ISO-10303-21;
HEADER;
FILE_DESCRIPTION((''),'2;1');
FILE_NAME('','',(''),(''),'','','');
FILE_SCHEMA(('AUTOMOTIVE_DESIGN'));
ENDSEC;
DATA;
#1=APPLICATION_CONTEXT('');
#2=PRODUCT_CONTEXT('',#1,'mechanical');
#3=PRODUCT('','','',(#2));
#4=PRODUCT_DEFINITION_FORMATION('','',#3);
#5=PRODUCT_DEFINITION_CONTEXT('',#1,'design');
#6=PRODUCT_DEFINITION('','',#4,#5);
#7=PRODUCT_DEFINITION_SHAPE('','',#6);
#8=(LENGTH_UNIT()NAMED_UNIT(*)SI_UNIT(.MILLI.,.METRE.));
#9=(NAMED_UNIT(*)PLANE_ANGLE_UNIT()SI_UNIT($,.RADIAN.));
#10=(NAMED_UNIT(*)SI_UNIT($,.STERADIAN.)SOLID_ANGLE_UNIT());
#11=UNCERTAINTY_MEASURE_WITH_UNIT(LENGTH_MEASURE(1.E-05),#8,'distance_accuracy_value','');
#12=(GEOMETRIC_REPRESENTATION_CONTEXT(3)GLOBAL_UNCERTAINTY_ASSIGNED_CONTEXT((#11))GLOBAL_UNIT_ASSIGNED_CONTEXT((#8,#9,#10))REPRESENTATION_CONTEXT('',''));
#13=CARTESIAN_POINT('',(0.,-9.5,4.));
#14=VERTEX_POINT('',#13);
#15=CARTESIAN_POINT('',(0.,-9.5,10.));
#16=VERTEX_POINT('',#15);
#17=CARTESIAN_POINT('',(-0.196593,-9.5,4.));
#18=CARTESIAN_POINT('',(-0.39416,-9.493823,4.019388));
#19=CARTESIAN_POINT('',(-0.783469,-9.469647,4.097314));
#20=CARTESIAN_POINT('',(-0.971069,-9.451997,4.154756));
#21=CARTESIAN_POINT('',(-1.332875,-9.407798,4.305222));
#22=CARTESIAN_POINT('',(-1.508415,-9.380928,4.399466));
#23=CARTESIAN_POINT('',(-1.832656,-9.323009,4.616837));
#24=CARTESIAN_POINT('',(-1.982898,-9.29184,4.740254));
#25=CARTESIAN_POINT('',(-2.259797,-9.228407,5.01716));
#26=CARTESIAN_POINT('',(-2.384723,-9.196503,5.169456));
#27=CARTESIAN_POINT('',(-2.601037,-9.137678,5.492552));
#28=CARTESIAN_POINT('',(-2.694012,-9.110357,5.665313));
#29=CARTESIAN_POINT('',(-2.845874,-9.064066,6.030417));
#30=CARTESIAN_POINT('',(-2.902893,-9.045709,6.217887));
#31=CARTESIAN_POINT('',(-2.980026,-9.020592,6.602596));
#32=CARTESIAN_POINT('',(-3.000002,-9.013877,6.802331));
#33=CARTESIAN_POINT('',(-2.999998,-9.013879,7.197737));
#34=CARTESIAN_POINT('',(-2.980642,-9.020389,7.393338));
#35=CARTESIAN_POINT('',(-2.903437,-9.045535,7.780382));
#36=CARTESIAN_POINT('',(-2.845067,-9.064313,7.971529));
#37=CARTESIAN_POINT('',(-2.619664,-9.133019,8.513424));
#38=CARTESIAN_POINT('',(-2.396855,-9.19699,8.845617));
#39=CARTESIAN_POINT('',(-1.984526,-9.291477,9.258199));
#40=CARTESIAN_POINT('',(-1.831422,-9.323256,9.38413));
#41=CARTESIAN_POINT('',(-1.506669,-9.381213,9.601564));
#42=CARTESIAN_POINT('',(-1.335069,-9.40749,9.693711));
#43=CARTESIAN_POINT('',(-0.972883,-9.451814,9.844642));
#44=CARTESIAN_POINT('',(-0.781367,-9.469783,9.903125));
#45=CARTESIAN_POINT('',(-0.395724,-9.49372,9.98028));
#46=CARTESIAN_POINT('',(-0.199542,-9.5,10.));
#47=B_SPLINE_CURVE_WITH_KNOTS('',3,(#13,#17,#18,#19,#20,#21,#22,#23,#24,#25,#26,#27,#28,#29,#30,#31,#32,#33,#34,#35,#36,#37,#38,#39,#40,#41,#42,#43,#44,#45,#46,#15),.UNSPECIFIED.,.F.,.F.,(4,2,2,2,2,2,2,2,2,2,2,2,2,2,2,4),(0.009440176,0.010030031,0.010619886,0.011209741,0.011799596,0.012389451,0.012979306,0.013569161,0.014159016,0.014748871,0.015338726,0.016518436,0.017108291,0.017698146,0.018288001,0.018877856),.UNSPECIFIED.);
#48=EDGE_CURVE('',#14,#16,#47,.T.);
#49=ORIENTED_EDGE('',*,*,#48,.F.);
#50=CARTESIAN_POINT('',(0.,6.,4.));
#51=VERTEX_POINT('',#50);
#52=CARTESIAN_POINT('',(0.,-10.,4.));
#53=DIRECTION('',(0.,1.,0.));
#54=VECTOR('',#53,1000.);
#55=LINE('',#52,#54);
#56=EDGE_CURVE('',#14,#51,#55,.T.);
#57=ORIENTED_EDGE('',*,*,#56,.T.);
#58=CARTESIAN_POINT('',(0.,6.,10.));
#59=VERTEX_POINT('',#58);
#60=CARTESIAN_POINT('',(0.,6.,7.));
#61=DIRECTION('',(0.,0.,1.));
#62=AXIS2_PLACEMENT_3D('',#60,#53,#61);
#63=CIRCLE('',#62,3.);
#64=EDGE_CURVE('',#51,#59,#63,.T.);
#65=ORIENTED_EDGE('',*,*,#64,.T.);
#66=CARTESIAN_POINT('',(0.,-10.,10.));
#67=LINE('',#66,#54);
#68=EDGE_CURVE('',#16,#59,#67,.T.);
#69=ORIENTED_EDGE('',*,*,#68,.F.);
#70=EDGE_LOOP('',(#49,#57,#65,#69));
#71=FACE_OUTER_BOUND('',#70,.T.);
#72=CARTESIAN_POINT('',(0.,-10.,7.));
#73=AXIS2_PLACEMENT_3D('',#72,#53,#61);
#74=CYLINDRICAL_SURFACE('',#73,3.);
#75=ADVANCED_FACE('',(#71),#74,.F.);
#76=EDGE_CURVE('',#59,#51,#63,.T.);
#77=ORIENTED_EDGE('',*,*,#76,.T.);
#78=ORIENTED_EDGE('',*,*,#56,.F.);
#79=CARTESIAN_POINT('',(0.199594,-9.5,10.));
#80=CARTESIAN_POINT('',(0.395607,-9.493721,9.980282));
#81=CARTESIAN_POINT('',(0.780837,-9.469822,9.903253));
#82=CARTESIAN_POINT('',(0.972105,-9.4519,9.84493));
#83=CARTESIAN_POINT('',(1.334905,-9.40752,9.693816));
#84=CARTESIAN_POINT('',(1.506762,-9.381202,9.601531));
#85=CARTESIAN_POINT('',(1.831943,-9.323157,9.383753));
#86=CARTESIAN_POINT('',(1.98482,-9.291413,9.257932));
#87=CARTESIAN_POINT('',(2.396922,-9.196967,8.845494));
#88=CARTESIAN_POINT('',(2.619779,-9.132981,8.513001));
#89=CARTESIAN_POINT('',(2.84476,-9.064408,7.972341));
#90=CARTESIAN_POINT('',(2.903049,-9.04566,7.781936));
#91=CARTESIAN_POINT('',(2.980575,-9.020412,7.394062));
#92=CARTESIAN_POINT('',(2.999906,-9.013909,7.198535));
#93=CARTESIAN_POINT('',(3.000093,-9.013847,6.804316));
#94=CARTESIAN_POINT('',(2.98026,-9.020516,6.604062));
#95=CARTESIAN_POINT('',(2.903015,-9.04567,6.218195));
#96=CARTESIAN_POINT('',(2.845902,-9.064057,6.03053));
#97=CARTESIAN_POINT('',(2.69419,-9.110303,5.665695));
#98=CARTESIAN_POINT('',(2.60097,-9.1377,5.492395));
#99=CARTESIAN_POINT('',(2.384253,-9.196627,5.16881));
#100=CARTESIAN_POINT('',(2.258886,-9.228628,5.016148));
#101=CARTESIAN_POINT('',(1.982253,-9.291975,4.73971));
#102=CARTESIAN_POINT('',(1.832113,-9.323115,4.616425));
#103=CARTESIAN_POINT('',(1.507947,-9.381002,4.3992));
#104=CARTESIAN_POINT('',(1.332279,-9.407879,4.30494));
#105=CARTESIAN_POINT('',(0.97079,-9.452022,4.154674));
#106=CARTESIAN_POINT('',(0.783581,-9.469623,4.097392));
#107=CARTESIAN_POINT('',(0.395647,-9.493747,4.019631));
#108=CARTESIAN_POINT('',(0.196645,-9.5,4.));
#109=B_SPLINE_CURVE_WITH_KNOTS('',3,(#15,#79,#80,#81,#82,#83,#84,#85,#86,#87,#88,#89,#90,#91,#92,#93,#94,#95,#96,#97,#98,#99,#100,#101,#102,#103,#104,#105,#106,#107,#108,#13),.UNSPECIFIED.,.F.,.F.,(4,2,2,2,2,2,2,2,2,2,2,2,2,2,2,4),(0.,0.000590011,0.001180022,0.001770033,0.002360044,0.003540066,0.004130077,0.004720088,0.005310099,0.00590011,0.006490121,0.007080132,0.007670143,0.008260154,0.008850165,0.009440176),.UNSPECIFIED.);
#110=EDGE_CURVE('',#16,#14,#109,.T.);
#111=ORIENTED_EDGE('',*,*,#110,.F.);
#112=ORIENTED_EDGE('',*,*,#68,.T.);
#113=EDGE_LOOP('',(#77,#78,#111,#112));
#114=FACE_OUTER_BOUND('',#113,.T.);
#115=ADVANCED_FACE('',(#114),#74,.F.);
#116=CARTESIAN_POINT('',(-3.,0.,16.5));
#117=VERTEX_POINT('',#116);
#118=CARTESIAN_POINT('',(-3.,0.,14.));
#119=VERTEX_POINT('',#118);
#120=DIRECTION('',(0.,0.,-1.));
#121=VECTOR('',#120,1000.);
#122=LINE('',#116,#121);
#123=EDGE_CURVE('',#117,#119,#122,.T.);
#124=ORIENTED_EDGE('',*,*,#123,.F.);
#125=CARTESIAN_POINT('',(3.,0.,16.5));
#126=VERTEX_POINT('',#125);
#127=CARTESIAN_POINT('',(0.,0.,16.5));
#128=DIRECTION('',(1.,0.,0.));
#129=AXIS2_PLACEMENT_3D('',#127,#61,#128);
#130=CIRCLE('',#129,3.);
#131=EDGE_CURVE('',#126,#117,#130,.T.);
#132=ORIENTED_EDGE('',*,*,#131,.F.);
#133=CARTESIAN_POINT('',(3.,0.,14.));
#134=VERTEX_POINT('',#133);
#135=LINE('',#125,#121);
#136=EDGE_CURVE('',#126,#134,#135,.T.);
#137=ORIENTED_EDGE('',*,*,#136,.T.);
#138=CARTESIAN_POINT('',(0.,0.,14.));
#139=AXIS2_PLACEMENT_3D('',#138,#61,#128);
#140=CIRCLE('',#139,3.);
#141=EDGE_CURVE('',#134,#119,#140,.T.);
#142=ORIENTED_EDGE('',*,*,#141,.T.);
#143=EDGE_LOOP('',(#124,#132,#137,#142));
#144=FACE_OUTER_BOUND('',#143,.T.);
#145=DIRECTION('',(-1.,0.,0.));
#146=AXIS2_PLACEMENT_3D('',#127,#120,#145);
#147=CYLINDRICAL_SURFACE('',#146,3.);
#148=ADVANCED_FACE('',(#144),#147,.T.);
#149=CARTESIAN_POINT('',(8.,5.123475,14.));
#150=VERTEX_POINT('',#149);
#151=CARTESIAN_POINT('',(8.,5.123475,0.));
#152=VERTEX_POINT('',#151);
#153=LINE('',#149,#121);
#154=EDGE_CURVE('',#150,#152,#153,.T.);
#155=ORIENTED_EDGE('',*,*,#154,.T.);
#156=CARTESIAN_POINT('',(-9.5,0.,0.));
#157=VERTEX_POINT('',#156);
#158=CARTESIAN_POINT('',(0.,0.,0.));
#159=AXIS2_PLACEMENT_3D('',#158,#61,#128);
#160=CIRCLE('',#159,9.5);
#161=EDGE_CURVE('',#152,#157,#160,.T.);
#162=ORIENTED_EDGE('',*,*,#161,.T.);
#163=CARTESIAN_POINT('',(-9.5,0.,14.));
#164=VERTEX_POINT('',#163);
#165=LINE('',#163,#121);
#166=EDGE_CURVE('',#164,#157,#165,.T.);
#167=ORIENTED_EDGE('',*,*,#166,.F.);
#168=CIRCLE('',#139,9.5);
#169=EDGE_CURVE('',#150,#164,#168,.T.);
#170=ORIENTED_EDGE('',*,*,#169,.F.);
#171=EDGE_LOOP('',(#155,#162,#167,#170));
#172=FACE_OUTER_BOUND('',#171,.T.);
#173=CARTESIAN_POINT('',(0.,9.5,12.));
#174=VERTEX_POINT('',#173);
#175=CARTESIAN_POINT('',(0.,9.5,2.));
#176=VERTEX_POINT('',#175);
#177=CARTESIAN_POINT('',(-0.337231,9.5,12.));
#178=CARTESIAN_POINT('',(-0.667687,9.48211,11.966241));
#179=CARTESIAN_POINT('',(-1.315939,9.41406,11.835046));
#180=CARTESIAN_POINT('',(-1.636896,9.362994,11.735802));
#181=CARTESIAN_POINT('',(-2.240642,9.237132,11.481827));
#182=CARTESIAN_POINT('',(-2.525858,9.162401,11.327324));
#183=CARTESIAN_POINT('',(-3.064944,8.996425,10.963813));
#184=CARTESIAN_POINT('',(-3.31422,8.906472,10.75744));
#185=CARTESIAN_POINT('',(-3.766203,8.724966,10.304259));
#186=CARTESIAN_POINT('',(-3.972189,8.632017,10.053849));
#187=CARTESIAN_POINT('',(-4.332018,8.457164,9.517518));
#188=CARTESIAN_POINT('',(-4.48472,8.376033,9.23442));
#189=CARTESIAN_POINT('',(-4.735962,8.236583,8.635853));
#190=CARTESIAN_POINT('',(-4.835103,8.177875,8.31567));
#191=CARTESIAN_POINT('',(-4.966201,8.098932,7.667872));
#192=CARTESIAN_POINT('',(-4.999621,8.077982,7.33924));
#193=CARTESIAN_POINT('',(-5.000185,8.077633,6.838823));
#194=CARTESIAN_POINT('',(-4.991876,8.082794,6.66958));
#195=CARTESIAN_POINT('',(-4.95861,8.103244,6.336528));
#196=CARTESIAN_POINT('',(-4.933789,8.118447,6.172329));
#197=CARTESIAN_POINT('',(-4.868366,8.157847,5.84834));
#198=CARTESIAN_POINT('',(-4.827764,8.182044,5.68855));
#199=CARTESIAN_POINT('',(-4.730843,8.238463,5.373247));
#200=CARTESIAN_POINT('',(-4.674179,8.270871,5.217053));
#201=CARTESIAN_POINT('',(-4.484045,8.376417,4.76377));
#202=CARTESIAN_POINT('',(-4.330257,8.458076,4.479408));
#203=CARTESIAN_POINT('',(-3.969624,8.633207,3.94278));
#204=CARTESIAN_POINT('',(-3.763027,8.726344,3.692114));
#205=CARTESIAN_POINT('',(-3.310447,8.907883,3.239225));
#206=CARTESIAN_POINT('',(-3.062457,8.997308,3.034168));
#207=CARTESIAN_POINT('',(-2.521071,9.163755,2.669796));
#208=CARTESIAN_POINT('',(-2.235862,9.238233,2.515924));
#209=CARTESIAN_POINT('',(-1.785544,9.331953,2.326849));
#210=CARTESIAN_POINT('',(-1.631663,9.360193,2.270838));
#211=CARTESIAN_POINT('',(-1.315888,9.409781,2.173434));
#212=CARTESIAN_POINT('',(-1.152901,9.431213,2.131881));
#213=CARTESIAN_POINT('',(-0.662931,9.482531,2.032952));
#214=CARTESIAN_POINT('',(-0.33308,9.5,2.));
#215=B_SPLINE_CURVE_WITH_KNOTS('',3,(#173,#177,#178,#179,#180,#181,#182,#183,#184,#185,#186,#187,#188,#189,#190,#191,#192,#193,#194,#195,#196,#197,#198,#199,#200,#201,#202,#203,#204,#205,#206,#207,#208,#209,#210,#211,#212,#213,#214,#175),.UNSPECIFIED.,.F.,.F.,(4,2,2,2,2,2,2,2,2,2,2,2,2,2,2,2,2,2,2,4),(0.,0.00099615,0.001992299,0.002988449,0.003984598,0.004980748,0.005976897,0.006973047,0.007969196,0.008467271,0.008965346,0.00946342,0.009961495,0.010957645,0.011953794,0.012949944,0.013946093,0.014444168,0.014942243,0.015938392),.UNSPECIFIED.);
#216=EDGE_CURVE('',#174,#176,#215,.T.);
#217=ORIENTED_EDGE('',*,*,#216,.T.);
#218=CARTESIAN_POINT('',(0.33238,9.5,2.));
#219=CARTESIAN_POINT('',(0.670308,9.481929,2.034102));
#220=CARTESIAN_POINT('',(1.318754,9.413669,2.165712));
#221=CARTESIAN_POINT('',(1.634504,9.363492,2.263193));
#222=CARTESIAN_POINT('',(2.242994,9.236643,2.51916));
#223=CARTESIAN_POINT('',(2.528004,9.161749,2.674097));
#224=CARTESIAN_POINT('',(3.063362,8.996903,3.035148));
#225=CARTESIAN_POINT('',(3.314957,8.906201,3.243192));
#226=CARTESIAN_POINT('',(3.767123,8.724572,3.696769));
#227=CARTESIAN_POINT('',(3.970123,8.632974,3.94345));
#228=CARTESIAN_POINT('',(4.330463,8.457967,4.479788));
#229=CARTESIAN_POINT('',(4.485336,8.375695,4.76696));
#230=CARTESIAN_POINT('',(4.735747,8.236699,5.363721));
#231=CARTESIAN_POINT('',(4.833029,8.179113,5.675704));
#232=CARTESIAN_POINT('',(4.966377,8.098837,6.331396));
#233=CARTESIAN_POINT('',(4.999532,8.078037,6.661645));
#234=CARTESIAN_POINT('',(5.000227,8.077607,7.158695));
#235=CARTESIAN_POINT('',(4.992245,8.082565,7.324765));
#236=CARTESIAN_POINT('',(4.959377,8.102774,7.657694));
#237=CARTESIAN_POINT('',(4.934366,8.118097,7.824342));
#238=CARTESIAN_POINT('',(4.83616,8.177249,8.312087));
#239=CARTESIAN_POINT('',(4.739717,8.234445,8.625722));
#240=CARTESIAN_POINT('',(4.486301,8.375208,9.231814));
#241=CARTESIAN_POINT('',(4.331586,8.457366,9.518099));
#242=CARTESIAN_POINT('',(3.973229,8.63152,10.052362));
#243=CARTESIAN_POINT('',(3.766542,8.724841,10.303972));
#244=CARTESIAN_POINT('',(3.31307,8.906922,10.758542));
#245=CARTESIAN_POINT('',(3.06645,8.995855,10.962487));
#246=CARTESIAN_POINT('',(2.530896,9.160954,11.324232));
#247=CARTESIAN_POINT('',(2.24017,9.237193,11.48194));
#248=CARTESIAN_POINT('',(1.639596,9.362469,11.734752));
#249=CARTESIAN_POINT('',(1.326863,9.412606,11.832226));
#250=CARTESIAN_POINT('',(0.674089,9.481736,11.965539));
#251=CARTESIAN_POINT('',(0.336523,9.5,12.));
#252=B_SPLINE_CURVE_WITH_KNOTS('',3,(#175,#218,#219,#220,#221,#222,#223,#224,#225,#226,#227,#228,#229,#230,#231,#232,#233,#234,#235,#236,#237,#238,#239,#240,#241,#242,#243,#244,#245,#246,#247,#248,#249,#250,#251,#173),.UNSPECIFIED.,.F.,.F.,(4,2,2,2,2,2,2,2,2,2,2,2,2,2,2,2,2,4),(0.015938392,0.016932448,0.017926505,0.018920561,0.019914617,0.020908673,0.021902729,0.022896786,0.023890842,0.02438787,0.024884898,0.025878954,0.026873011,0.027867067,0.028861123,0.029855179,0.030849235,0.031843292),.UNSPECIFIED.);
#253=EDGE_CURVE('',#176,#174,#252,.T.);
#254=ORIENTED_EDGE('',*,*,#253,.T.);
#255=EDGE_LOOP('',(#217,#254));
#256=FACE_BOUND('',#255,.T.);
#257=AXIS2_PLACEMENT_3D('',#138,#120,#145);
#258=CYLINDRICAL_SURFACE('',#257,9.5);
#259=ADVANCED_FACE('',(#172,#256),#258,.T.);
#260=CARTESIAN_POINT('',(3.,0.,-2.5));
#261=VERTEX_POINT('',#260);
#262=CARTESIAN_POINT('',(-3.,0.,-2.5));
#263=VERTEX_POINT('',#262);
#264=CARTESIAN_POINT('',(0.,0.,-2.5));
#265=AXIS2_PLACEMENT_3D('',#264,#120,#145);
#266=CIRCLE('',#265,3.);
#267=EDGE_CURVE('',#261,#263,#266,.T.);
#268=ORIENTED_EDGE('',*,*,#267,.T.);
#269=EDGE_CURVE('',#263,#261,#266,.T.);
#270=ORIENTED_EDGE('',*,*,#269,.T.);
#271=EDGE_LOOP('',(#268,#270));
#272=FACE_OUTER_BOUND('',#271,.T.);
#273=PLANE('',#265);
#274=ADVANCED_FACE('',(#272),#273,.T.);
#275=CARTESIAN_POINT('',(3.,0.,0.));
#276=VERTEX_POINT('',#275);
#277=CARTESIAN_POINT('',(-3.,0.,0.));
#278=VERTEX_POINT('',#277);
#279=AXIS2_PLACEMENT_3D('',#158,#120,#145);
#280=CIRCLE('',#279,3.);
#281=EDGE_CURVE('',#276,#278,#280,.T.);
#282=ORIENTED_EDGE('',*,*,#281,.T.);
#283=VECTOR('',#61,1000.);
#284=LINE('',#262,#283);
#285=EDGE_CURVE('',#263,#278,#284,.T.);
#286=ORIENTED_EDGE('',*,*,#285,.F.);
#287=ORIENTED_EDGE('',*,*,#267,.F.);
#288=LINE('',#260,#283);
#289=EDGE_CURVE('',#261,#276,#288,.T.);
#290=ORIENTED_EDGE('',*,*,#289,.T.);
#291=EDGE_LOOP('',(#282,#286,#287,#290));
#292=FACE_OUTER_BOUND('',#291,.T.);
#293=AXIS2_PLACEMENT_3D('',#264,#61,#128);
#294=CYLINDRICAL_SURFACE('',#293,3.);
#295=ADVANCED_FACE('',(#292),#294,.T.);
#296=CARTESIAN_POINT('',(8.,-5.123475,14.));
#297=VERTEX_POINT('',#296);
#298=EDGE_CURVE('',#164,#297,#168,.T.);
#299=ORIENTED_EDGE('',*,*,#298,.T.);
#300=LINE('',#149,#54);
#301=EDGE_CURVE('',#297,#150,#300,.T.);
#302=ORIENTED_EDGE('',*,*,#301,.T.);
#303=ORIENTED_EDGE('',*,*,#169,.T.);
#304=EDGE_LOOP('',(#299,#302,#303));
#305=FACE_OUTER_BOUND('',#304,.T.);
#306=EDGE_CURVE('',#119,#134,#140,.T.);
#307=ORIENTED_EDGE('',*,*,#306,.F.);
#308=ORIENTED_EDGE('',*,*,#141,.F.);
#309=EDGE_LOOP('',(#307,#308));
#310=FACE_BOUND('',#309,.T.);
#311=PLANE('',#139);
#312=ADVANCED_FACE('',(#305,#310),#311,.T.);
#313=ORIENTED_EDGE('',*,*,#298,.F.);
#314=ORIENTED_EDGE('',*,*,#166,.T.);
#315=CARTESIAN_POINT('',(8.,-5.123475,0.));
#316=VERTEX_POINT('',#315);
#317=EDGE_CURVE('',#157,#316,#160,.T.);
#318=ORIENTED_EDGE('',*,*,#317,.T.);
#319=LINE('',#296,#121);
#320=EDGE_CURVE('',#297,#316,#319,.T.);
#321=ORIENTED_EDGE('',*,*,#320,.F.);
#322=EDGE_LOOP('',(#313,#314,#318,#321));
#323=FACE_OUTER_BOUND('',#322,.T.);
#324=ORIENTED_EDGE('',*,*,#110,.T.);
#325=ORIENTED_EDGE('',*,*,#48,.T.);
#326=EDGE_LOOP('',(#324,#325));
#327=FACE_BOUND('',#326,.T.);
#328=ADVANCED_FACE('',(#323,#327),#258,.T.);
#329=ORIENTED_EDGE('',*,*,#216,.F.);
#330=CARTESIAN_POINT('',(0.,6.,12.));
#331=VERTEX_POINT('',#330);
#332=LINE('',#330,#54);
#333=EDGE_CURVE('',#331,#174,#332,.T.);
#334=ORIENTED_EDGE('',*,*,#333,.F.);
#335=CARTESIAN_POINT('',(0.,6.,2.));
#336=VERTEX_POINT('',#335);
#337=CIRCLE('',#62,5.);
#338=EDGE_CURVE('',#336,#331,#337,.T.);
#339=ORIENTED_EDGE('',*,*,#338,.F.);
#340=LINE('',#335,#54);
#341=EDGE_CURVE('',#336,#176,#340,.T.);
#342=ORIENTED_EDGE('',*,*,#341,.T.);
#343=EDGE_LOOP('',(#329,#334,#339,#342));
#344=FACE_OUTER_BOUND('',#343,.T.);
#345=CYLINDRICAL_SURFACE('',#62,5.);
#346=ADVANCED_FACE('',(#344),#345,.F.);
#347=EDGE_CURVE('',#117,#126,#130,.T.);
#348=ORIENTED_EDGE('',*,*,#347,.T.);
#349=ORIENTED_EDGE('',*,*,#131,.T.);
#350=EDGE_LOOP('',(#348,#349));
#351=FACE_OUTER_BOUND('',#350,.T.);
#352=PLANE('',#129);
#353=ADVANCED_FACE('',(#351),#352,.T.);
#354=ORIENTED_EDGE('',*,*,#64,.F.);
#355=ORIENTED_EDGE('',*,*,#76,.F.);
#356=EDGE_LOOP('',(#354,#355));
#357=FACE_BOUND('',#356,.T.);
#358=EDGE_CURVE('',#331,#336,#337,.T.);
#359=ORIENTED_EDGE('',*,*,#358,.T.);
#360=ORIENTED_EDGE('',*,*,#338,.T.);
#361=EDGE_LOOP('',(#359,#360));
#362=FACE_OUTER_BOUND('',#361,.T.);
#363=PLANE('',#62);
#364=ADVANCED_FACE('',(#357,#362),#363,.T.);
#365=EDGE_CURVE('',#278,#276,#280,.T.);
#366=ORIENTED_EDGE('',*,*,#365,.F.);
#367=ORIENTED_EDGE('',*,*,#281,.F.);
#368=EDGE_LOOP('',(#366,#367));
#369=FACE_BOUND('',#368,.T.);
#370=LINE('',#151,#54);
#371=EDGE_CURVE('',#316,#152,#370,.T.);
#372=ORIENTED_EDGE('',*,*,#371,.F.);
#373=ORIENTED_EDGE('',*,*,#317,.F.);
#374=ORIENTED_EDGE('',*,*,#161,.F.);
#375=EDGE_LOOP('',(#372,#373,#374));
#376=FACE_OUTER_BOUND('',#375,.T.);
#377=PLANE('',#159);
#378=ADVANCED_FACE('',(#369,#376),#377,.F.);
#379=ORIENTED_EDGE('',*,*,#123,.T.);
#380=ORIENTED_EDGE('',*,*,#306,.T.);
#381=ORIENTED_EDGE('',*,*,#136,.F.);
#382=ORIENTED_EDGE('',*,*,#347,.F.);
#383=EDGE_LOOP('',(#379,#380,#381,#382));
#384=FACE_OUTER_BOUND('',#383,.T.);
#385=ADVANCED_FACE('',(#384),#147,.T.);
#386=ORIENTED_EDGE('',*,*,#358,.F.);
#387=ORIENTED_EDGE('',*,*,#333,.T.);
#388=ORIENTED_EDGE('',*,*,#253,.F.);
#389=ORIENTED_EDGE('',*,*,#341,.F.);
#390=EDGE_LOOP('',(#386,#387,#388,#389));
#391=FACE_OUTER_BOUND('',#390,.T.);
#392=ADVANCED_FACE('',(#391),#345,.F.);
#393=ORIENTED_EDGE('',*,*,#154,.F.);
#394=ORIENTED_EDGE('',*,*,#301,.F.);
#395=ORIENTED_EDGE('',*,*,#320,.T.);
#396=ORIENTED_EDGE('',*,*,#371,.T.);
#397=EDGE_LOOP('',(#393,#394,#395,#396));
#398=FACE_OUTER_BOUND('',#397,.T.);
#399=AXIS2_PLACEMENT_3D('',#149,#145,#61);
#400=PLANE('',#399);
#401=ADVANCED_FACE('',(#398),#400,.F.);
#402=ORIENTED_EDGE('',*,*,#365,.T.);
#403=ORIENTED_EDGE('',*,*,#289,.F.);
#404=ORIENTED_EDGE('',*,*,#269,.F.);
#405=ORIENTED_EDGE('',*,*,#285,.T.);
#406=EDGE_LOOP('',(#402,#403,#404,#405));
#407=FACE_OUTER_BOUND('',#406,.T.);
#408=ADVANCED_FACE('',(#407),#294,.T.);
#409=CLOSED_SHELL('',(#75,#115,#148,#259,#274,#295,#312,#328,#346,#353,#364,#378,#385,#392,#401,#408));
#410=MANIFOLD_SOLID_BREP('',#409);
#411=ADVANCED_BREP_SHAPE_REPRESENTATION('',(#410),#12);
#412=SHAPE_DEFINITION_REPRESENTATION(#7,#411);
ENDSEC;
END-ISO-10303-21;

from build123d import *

# Parameters (mm, degrees)
BUSHING_BODY_DEPTH          = 14
FRONT_PIVOT_PIN_PROFILE_6_R = 3
FRONT_PIVOT_PIN_6_DEPTH     = 2.5
REAR_START                  = 2.5
REAR_PIVOT_PIN_PROFILE_6_R  = 3
REAR_PIVOT_PIN_6_DEPTH      = 2.5
CROSS_COUNTERBORE_PROFILE_R = 5
CROSS_COUNTERBORE_DEPTH     = 4
CROSS_HOLE_PROFILE_6_R      = 3
CROSS_HOLE_6_DEPTH          = 16


with BuildPart() as part:
    # Body Profile Ø19 D-Flat → Bushing Body (new body)
    with BuildSketch(Plane.XY):
        with BuildLine():
            Line((8, 5.123475383), (8, -5.123475383))
            ThreePointArc((8, -5.123475383), (-9.5, 0), (8, 5.123475383))
        make_face()
    extrude(amount=BUSHING_BODY_DEPTH)

    # Front Pivot Pin Profile Ø6 → Front Pivot Pin Ø6 (add)
    with BuildSketch(Plane.XY.offset(14)):
        Circle(FRONT_PIVOT_PIN_PROFILE_6_R)
    extrude(amount=FRONT_PIVOT_PIN_6_DEPTH)

    # Rear Pivot Pin Profile Ø6 → Rear Pivot Pin Ø6 (add)
    with BuildSketch(Plane(origin=(0, 0, 0), x_dir=(-1, 0, 0), z_dir=(0, 0, -1)).offset(REAR_START)):
        with Locations(Location((0, 0, 0), (0, 0, 180))):
            Circle(REAR_PIVOT_PIN_PROFILE_6_R)
    extrude(amount=-REAR_PIVOT_PIN_6_DEPTH)

    # Cross Counterbore Profile → Cross Counterbore (cut)
    with BuildSketch(Plane(origin=(0, 10, 0), x_dir=(1, 0, 0), z_dir=(0, 1, 0))):
        with Locations(Location((0, -7, 0), (0, 0, 270))):
            Circle(CROSS_COUNTERBORE_PROFILE_R)
    extrude(amount=-CROSS_COUNTERBORE_DEPTH, mode=Mode.SUBTRACT)

    # Cross Hole Profile Ø6 → Cross Hole Ø6 (cut)
    with BuildSketch(Plane(origin=(0, 6, 0), x_dir=(1, 0, 0), z_dir=(0, 1, 0))):
        with Locations(Location((0, -7, 0), (0, 0, 270))):
            Circle(CROSS_HOLE_PROFILE_6_R)
    extrude(amount=-CROSS_HOLE_6_DEPTH, mode=Mode.SUBTRACT)


solid = part.part
